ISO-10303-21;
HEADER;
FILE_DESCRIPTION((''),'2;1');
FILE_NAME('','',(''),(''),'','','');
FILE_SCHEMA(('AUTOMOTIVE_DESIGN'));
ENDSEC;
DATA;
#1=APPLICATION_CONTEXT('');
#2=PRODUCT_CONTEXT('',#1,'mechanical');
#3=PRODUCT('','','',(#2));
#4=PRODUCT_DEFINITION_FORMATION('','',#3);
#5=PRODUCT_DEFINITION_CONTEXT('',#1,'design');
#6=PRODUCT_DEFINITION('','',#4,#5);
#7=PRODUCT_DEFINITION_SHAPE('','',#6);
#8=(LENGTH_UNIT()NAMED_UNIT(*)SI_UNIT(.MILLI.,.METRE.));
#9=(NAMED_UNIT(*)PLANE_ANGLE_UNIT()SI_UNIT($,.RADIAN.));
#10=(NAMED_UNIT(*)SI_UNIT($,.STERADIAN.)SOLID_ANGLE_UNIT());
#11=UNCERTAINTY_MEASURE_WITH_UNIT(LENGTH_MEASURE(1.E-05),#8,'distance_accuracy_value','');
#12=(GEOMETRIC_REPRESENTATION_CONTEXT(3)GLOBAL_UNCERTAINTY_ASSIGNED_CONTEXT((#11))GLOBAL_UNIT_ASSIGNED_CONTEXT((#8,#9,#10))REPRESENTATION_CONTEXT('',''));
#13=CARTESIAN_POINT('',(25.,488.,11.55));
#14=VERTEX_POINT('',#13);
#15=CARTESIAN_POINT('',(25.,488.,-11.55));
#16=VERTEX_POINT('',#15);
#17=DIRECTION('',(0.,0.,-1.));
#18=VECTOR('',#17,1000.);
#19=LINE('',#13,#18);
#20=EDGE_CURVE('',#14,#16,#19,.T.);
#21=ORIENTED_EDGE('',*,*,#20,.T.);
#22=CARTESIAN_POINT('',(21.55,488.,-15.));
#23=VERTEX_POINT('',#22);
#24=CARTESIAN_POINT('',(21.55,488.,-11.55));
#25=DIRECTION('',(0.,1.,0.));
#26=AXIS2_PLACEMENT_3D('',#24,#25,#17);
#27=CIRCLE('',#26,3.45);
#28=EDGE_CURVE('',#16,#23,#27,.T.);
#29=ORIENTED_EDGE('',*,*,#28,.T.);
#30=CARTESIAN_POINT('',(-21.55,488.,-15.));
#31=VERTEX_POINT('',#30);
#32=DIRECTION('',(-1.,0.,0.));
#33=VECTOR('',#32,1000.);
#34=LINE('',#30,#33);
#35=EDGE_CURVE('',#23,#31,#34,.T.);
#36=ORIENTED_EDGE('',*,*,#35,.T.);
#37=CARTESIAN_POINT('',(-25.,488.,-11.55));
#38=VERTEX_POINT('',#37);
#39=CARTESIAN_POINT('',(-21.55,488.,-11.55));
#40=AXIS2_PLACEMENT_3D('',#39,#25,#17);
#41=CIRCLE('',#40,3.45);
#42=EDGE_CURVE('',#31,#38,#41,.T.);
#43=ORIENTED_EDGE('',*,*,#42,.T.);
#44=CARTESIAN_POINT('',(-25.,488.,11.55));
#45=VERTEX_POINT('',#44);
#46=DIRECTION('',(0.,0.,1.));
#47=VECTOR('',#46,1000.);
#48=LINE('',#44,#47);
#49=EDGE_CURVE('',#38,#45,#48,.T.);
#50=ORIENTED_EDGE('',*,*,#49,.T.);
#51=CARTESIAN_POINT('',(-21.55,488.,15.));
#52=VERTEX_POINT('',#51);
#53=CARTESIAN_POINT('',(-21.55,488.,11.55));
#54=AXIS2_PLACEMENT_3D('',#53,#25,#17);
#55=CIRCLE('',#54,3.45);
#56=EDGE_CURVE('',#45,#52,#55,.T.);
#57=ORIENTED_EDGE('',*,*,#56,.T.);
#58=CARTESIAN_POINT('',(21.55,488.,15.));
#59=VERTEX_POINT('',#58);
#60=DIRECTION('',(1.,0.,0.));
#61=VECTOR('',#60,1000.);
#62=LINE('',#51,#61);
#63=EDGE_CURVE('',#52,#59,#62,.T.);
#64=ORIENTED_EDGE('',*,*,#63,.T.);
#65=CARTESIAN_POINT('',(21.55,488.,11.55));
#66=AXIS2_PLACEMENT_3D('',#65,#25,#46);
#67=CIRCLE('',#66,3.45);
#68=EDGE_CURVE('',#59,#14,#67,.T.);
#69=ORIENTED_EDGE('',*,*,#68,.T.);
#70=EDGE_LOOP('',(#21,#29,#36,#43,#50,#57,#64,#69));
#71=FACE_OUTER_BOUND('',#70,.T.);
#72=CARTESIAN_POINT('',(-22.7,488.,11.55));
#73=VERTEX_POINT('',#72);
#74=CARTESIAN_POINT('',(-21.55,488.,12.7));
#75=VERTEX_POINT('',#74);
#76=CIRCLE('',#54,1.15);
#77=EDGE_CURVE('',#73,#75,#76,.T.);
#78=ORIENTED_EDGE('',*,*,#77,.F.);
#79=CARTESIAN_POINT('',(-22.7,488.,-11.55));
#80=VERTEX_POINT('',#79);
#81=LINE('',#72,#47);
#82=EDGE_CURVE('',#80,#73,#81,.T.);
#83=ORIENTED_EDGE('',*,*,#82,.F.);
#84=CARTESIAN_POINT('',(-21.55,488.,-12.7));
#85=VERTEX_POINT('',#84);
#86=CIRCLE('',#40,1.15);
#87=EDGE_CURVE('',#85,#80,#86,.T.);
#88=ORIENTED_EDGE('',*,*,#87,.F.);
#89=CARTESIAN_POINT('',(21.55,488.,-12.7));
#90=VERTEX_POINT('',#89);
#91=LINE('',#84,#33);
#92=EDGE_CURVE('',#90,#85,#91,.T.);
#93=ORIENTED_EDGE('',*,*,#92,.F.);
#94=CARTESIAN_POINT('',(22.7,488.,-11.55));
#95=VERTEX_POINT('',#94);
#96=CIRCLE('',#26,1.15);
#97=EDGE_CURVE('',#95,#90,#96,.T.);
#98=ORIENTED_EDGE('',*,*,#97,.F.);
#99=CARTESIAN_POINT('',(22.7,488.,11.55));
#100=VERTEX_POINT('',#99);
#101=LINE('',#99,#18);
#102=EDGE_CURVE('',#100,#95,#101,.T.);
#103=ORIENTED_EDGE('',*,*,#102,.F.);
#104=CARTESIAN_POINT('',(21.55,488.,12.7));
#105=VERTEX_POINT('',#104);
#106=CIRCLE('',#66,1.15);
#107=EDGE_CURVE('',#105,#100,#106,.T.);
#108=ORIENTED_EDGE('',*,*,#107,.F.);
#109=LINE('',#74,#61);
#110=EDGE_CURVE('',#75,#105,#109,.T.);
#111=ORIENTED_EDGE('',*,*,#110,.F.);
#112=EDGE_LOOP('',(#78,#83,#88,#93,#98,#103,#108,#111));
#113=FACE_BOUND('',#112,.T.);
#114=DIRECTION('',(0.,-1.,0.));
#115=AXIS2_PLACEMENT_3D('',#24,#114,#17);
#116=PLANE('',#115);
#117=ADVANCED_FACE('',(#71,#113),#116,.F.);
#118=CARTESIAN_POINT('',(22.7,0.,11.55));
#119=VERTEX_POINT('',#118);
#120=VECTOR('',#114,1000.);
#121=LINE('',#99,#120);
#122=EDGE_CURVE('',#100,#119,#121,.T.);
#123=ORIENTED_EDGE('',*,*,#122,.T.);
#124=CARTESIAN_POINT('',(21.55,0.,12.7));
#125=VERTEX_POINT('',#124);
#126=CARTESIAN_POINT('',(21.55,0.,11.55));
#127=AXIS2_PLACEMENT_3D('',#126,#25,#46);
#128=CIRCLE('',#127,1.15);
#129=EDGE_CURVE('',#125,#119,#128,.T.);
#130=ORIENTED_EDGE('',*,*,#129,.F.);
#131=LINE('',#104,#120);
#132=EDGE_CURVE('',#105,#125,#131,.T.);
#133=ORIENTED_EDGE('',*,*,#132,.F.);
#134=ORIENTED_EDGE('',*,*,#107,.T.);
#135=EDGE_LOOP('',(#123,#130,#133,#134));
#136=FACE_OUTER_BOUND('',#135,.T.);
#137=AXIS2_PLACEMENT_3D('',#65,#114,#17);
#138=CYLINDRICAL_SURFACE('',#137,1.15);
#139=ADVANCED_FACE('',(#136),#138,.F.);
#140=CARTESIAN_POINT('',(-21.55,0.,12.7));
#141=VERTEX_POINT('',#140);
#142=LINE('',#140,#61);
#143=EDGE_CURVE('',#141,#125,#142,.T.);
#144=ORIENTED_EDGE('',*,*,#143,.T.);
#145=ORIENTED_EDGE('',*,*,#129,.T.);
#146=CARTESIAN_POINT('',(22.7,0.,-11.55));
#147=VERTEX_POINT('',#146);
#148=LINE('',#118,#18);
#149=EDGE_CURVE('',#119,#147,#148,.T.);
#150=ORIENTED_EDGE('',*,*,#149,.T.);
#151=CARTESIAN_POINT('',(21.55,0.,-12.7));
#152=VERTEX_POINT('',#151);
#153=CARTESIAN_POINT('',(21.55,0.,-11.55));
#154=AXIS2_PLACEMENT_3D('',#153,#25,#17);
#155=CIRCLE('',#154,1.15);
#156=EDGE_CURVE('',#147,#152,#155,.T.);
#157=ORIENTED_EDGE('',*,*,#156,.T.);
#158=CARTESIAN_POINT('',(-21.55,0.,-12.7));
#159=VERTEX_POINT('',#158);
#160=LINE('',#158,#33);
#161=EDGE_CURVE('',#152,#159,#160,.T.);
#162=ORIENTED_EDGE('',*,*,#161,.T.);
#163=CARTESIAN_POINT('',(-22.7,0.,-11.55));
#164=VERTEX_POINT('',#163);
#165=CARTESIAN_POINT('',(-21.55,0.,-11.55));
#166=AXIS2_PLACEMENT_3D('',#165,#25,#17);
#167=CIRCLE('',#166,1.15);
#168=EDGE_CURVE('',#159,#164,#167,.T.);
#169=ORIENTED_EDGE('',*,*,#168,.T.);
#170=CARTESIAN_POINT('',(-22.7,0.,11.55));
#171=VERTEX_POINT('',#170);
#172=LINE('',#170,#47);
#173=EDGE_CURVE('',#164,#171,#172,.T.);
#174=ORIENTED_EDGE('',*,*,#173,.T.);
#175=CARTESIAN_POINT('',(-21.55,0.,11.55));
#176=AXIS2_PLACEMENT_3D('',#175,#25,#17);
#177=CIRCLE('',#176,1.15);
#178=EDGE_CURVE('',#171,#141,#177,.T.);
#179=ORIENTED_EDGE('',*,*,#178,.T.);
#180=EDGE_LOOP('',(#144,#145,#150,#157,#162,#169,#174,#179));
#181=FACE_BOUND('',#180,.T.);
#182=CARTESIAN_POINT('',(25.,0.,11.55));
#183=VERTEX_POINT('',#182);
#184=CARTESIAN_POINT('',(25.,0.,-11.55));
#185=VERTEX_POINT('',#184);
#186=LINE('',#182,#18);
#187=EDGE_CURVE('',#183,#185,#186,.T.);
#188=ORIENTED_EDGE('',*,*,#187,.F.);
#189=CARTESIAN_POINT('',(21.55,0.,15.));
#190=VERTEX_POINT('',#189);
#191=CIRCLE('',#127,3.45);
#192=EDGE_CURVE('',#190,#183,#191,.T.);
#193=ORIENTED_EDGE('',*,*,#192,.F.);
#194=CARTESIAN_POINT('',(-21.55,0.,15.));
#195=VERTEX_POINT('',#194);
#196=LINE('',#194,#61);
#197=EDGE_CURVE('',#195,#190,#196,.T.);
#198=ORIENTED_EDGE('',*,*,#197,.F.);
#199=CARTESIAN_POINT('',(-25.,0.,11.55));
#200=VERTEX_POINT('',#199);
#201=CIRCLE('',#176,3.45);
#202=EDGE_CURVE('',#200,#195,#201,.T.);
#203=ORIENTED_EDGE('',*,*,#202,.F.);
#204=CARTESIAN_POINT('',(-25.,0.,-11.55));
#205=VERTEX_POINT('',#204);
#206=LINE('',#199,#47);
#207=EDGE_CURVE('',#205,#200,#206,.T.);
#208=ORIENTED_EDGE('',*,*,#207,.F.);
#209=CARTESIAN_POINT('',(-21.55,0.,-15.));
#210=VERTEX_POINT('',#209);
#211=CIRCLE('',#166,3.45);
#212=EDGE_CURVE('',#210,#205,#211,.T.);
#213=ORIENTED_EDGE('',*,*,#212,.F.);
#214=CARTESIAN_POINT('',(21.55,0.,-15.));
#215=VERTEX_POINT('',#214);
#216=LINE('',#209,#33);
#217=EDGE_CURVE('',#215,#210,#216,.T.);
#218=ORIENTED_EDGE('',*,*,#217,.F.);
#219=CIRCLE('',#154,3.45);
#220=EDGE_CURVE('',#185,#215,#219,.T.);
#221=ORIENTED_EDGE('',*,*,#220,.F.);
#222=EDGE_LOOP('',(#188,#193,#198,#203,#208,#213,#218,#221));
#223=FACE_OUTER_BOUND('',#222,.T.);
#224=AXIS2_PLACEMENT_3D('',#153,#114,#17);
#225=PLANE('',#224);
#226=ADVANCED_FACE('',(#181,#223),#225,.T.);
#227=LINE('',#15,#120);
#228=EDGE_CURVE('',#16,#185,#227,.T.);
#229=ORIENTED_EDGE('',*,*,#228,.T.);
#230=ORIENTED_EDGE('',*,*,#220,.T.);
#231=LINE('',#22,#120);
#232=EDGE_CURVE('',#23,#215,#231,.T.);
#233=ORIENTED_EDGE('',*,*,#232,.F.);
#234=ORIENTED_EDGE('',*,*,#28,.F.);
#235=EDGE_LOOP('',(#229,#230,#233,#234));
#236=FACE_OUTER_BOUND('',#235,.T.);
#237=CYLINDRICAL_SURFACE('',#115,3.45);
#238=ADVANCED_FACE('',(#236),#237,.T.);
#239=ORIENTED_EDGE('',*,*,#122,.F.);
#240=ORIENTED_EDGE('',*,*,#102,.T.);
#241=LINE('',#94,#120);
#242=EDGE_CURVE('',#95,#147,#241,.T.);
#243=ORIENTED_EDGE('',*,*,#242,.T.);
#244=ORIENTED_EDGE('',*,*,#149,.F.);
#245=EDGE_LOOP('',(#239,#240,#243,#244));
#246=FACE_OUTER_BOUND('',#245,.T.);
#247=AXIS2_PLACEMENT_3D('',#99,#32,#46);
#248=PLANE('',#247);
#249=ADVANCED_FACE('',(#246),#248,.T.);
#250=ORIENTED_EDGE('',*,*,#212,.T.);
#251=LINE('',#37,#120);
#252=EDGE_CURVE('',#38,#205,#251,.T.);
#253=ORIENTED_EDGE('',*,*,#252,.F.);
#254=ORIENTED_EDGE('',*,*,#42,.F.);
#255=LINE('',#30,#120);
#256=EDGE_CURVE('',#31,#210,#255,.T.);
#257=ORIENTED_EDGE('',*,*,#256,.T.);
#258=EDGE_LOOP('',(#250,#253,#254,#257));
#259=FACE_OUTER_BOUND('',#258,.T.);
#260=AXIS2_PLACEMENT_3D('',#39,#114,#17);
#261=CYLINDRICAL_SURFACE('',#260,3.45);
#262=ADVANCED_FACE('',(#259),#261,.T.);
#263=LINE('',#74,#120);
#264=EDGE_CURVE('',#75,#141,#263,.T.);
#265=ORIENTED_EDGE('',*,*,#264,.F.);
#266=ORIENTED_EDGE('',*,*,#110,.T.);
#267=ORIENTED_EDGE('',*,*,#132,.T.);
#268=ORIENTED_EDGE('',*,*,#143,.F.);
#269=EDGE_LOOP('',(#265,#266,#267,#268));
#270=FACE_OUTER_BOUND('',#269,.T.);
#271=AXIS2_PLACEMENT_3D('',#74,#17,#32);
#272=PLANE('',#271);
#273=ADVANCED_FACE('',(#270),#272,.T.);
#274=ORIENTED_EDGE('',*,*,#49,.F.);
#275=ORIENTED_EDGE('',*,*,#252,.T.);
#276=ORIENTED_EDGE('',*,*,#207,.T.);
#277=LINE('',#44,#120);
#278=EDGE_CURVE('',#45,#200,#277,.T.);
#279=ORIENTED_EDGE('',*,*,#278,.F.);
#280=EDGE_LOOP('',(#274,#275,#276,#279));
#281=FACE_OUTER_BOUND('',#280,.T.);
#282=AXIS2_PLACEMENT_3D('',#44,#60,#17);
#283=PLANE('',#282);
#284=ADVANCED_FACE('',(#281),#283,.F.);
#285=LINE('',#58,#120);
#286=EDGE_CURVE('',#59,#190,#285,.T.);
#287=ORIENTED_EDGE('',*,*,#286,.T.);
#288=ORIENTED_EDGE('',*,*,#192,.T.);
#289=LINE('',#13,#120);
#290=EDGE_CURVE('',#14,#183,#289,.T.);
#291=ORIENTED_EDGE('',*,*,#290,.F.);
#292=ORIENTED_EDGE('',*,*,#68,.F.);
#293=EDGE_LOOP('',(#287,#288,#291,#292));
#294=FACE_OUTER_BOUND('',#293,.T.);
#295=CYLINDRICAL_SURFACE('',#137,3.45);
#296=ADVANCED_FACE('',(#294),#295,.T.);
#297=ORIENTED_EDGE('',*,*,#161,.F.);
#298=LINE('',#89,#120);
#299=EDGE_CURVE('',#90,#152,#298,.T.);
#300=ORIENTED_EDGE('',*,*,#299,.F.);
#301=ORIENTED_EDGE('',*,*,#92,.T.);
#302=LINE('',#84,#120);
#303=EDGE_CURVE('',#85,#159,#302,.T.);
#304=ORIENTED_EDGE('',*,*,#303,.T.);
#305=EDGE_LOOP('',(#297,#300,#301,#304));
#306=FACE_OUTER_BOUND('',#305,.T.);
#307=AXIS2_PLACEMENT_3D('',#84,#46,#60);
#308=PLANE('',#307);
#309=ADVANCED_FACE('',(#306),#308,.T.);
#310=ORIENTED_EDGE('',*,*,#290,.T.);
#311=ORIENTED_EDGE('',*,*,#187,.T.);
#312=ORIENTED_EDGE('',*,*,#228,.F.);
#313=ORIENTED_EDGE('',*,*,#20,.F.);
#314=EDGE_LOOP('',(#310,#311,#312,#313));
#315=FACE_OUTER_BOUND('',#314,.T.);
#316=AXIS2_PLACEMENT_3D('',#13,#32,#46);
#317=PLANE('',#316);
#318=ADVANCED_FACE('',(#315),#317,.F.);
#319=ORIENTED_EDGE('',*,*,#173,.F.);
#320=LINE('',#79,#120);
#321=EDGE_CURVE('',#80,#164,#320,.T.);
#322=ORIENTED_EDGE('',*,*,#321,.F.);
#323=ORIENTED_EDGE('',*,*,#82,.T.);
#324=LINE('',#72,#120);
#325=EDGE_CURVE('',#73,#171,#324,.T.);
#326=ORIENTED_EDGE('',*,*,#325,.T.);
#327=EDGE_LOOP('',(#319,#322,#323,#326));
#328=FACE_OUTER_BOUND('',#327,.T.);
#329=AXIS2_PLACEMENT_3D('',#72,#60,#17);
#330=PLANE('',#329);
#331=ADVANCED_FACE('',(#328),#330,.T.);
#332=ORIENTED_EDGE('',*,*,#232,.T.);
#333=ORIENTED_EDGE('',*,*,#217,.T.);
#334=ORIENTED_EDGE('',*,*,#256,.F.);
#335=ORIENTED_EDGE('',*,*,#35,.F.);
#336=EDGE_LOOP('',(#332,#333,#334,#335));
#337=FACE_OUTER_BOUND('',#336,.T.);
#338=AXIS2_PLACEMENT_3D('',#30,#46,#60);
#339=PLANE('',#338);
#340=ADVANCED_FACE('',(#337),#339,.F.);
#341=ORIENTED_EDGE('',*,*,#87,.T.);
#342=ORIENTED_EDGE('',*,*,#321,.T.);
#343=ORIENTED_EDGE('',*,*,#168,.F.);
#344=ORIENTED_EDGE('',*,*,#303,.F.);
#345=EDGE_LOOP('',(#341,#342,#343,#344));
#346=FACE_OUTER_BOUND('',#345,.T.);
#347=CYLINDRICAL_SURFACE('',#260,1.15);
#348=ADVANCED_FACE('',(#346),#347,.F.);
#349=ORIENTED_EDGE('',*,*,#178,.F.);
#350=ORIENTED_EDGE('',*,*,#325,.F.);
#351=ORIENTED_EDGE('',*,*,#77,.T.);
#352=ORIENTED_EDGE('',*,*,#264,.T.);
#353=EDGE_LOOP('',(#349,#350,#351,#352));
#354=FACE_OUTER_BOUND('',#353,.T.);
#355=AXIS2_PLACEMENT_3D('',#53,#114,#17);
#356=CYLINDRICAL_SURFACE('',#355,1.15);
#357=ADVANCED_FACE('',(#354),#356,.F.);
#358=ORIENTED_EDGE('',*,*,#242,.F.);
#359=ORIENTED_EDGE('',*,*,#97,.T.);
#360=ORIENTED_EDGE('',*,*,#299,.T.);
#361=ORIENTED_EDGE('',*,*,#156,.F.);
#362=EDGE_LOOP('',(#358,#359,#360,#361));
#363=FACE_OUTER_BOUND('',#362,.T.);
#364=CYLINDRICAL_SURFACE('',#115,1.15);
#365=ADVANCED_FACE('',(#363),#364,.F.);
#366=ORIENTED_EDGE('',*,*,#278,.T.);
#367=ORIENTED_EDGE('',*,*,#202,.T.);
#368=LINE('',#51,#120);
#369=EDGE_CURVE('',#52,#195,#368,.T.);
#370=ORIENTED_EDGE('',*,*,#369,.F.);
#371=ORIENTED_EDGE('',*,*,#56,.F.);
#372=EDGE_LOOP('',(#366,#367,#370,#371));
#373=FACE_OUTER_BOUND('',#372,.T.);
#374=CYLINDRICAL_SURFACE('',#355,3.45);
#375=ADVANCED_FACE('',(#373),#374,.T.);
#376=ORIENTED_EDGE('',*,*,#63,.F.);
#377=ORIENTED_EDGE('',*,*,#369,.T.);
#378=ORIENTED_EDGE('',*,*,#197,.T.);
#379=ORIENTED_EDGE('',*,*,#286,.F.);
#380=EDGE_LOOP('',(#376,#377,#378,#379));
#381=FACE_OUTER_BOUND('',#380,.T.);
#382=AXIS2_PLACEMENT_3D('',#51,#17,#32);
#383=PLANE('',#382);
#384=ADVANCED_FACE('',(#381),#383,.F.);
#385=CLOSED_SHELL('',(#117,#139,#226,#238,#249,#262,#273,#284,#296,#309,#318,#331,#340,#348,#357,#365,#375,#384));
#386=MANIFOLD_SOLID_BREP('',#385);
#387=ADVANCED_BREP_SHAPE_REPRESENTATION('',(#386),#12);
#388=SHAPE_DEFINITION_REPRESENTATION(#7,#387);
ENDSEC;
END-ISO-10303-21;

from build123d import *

# Parameters (mm, degrees)
BOSS_EXTRUDE1_DEPTH = 488


with BuildPart() as part:
    # Sketch1 → Boss-Extrude1 (new body)
    with BuildSketch(Plane(origin=(0, 0, 0), x_dir=(1, 0, 0), z_dir=(0, 1, 0))):
        with BuildLine():
            Line((-21.55, -15), (21.55, -15))
            ThreePointArc((21.55, -15), (23.989518395, -13.989518395), (25, -11.55))
            Line((25, -11.55), (25, 11.55))
            ThreePointArc((25, 11.55), (23.989518395, 13.989518395), (21.55, 15))
            Line((21.55, 15), (-21.55, 15))
            ThreePointArc((-21.55, 15), (-23.989518395, 13.989518395), (-25, 11.55))
            Line((-25, 11.55), (-25, -11.55))
            ThreePointArc((-25, -11.55), (-23.989518395, -13.989518395), (-21.55, -15))
        make_face()
        with BuildLine():
            Line((-21.55, -12.7), (21.55, -12.7))
            ThreePointArc((21.55, -12.7), (22.363172798, -12.363172798), (22.7, -11.55))
            Line((22.7, -11.55), (22.7, 11.55))
            ThreePointArc((22.7, 11.55), (22.363172798, 12.363172798), (21.55, 12.7))
            Line((21.55, 12.7), (-21.55, 12.7))
            ThreePointArc((-21.55, 12.7), (-22.363172798, 12.363172798), (-22.7, 11.55))
            Line((-22.7, 11.55), (-22.7, -11.55))
            ThreePointArc((-22.7, -11.55), (-22.363172798, -12.363172798), (-21.55, -12.7))
        make_face(mode=Mode.SUBTRACT)
    extrude(amount=BOSS_EXTRUDE1_DEPTH)


solid = part.part
